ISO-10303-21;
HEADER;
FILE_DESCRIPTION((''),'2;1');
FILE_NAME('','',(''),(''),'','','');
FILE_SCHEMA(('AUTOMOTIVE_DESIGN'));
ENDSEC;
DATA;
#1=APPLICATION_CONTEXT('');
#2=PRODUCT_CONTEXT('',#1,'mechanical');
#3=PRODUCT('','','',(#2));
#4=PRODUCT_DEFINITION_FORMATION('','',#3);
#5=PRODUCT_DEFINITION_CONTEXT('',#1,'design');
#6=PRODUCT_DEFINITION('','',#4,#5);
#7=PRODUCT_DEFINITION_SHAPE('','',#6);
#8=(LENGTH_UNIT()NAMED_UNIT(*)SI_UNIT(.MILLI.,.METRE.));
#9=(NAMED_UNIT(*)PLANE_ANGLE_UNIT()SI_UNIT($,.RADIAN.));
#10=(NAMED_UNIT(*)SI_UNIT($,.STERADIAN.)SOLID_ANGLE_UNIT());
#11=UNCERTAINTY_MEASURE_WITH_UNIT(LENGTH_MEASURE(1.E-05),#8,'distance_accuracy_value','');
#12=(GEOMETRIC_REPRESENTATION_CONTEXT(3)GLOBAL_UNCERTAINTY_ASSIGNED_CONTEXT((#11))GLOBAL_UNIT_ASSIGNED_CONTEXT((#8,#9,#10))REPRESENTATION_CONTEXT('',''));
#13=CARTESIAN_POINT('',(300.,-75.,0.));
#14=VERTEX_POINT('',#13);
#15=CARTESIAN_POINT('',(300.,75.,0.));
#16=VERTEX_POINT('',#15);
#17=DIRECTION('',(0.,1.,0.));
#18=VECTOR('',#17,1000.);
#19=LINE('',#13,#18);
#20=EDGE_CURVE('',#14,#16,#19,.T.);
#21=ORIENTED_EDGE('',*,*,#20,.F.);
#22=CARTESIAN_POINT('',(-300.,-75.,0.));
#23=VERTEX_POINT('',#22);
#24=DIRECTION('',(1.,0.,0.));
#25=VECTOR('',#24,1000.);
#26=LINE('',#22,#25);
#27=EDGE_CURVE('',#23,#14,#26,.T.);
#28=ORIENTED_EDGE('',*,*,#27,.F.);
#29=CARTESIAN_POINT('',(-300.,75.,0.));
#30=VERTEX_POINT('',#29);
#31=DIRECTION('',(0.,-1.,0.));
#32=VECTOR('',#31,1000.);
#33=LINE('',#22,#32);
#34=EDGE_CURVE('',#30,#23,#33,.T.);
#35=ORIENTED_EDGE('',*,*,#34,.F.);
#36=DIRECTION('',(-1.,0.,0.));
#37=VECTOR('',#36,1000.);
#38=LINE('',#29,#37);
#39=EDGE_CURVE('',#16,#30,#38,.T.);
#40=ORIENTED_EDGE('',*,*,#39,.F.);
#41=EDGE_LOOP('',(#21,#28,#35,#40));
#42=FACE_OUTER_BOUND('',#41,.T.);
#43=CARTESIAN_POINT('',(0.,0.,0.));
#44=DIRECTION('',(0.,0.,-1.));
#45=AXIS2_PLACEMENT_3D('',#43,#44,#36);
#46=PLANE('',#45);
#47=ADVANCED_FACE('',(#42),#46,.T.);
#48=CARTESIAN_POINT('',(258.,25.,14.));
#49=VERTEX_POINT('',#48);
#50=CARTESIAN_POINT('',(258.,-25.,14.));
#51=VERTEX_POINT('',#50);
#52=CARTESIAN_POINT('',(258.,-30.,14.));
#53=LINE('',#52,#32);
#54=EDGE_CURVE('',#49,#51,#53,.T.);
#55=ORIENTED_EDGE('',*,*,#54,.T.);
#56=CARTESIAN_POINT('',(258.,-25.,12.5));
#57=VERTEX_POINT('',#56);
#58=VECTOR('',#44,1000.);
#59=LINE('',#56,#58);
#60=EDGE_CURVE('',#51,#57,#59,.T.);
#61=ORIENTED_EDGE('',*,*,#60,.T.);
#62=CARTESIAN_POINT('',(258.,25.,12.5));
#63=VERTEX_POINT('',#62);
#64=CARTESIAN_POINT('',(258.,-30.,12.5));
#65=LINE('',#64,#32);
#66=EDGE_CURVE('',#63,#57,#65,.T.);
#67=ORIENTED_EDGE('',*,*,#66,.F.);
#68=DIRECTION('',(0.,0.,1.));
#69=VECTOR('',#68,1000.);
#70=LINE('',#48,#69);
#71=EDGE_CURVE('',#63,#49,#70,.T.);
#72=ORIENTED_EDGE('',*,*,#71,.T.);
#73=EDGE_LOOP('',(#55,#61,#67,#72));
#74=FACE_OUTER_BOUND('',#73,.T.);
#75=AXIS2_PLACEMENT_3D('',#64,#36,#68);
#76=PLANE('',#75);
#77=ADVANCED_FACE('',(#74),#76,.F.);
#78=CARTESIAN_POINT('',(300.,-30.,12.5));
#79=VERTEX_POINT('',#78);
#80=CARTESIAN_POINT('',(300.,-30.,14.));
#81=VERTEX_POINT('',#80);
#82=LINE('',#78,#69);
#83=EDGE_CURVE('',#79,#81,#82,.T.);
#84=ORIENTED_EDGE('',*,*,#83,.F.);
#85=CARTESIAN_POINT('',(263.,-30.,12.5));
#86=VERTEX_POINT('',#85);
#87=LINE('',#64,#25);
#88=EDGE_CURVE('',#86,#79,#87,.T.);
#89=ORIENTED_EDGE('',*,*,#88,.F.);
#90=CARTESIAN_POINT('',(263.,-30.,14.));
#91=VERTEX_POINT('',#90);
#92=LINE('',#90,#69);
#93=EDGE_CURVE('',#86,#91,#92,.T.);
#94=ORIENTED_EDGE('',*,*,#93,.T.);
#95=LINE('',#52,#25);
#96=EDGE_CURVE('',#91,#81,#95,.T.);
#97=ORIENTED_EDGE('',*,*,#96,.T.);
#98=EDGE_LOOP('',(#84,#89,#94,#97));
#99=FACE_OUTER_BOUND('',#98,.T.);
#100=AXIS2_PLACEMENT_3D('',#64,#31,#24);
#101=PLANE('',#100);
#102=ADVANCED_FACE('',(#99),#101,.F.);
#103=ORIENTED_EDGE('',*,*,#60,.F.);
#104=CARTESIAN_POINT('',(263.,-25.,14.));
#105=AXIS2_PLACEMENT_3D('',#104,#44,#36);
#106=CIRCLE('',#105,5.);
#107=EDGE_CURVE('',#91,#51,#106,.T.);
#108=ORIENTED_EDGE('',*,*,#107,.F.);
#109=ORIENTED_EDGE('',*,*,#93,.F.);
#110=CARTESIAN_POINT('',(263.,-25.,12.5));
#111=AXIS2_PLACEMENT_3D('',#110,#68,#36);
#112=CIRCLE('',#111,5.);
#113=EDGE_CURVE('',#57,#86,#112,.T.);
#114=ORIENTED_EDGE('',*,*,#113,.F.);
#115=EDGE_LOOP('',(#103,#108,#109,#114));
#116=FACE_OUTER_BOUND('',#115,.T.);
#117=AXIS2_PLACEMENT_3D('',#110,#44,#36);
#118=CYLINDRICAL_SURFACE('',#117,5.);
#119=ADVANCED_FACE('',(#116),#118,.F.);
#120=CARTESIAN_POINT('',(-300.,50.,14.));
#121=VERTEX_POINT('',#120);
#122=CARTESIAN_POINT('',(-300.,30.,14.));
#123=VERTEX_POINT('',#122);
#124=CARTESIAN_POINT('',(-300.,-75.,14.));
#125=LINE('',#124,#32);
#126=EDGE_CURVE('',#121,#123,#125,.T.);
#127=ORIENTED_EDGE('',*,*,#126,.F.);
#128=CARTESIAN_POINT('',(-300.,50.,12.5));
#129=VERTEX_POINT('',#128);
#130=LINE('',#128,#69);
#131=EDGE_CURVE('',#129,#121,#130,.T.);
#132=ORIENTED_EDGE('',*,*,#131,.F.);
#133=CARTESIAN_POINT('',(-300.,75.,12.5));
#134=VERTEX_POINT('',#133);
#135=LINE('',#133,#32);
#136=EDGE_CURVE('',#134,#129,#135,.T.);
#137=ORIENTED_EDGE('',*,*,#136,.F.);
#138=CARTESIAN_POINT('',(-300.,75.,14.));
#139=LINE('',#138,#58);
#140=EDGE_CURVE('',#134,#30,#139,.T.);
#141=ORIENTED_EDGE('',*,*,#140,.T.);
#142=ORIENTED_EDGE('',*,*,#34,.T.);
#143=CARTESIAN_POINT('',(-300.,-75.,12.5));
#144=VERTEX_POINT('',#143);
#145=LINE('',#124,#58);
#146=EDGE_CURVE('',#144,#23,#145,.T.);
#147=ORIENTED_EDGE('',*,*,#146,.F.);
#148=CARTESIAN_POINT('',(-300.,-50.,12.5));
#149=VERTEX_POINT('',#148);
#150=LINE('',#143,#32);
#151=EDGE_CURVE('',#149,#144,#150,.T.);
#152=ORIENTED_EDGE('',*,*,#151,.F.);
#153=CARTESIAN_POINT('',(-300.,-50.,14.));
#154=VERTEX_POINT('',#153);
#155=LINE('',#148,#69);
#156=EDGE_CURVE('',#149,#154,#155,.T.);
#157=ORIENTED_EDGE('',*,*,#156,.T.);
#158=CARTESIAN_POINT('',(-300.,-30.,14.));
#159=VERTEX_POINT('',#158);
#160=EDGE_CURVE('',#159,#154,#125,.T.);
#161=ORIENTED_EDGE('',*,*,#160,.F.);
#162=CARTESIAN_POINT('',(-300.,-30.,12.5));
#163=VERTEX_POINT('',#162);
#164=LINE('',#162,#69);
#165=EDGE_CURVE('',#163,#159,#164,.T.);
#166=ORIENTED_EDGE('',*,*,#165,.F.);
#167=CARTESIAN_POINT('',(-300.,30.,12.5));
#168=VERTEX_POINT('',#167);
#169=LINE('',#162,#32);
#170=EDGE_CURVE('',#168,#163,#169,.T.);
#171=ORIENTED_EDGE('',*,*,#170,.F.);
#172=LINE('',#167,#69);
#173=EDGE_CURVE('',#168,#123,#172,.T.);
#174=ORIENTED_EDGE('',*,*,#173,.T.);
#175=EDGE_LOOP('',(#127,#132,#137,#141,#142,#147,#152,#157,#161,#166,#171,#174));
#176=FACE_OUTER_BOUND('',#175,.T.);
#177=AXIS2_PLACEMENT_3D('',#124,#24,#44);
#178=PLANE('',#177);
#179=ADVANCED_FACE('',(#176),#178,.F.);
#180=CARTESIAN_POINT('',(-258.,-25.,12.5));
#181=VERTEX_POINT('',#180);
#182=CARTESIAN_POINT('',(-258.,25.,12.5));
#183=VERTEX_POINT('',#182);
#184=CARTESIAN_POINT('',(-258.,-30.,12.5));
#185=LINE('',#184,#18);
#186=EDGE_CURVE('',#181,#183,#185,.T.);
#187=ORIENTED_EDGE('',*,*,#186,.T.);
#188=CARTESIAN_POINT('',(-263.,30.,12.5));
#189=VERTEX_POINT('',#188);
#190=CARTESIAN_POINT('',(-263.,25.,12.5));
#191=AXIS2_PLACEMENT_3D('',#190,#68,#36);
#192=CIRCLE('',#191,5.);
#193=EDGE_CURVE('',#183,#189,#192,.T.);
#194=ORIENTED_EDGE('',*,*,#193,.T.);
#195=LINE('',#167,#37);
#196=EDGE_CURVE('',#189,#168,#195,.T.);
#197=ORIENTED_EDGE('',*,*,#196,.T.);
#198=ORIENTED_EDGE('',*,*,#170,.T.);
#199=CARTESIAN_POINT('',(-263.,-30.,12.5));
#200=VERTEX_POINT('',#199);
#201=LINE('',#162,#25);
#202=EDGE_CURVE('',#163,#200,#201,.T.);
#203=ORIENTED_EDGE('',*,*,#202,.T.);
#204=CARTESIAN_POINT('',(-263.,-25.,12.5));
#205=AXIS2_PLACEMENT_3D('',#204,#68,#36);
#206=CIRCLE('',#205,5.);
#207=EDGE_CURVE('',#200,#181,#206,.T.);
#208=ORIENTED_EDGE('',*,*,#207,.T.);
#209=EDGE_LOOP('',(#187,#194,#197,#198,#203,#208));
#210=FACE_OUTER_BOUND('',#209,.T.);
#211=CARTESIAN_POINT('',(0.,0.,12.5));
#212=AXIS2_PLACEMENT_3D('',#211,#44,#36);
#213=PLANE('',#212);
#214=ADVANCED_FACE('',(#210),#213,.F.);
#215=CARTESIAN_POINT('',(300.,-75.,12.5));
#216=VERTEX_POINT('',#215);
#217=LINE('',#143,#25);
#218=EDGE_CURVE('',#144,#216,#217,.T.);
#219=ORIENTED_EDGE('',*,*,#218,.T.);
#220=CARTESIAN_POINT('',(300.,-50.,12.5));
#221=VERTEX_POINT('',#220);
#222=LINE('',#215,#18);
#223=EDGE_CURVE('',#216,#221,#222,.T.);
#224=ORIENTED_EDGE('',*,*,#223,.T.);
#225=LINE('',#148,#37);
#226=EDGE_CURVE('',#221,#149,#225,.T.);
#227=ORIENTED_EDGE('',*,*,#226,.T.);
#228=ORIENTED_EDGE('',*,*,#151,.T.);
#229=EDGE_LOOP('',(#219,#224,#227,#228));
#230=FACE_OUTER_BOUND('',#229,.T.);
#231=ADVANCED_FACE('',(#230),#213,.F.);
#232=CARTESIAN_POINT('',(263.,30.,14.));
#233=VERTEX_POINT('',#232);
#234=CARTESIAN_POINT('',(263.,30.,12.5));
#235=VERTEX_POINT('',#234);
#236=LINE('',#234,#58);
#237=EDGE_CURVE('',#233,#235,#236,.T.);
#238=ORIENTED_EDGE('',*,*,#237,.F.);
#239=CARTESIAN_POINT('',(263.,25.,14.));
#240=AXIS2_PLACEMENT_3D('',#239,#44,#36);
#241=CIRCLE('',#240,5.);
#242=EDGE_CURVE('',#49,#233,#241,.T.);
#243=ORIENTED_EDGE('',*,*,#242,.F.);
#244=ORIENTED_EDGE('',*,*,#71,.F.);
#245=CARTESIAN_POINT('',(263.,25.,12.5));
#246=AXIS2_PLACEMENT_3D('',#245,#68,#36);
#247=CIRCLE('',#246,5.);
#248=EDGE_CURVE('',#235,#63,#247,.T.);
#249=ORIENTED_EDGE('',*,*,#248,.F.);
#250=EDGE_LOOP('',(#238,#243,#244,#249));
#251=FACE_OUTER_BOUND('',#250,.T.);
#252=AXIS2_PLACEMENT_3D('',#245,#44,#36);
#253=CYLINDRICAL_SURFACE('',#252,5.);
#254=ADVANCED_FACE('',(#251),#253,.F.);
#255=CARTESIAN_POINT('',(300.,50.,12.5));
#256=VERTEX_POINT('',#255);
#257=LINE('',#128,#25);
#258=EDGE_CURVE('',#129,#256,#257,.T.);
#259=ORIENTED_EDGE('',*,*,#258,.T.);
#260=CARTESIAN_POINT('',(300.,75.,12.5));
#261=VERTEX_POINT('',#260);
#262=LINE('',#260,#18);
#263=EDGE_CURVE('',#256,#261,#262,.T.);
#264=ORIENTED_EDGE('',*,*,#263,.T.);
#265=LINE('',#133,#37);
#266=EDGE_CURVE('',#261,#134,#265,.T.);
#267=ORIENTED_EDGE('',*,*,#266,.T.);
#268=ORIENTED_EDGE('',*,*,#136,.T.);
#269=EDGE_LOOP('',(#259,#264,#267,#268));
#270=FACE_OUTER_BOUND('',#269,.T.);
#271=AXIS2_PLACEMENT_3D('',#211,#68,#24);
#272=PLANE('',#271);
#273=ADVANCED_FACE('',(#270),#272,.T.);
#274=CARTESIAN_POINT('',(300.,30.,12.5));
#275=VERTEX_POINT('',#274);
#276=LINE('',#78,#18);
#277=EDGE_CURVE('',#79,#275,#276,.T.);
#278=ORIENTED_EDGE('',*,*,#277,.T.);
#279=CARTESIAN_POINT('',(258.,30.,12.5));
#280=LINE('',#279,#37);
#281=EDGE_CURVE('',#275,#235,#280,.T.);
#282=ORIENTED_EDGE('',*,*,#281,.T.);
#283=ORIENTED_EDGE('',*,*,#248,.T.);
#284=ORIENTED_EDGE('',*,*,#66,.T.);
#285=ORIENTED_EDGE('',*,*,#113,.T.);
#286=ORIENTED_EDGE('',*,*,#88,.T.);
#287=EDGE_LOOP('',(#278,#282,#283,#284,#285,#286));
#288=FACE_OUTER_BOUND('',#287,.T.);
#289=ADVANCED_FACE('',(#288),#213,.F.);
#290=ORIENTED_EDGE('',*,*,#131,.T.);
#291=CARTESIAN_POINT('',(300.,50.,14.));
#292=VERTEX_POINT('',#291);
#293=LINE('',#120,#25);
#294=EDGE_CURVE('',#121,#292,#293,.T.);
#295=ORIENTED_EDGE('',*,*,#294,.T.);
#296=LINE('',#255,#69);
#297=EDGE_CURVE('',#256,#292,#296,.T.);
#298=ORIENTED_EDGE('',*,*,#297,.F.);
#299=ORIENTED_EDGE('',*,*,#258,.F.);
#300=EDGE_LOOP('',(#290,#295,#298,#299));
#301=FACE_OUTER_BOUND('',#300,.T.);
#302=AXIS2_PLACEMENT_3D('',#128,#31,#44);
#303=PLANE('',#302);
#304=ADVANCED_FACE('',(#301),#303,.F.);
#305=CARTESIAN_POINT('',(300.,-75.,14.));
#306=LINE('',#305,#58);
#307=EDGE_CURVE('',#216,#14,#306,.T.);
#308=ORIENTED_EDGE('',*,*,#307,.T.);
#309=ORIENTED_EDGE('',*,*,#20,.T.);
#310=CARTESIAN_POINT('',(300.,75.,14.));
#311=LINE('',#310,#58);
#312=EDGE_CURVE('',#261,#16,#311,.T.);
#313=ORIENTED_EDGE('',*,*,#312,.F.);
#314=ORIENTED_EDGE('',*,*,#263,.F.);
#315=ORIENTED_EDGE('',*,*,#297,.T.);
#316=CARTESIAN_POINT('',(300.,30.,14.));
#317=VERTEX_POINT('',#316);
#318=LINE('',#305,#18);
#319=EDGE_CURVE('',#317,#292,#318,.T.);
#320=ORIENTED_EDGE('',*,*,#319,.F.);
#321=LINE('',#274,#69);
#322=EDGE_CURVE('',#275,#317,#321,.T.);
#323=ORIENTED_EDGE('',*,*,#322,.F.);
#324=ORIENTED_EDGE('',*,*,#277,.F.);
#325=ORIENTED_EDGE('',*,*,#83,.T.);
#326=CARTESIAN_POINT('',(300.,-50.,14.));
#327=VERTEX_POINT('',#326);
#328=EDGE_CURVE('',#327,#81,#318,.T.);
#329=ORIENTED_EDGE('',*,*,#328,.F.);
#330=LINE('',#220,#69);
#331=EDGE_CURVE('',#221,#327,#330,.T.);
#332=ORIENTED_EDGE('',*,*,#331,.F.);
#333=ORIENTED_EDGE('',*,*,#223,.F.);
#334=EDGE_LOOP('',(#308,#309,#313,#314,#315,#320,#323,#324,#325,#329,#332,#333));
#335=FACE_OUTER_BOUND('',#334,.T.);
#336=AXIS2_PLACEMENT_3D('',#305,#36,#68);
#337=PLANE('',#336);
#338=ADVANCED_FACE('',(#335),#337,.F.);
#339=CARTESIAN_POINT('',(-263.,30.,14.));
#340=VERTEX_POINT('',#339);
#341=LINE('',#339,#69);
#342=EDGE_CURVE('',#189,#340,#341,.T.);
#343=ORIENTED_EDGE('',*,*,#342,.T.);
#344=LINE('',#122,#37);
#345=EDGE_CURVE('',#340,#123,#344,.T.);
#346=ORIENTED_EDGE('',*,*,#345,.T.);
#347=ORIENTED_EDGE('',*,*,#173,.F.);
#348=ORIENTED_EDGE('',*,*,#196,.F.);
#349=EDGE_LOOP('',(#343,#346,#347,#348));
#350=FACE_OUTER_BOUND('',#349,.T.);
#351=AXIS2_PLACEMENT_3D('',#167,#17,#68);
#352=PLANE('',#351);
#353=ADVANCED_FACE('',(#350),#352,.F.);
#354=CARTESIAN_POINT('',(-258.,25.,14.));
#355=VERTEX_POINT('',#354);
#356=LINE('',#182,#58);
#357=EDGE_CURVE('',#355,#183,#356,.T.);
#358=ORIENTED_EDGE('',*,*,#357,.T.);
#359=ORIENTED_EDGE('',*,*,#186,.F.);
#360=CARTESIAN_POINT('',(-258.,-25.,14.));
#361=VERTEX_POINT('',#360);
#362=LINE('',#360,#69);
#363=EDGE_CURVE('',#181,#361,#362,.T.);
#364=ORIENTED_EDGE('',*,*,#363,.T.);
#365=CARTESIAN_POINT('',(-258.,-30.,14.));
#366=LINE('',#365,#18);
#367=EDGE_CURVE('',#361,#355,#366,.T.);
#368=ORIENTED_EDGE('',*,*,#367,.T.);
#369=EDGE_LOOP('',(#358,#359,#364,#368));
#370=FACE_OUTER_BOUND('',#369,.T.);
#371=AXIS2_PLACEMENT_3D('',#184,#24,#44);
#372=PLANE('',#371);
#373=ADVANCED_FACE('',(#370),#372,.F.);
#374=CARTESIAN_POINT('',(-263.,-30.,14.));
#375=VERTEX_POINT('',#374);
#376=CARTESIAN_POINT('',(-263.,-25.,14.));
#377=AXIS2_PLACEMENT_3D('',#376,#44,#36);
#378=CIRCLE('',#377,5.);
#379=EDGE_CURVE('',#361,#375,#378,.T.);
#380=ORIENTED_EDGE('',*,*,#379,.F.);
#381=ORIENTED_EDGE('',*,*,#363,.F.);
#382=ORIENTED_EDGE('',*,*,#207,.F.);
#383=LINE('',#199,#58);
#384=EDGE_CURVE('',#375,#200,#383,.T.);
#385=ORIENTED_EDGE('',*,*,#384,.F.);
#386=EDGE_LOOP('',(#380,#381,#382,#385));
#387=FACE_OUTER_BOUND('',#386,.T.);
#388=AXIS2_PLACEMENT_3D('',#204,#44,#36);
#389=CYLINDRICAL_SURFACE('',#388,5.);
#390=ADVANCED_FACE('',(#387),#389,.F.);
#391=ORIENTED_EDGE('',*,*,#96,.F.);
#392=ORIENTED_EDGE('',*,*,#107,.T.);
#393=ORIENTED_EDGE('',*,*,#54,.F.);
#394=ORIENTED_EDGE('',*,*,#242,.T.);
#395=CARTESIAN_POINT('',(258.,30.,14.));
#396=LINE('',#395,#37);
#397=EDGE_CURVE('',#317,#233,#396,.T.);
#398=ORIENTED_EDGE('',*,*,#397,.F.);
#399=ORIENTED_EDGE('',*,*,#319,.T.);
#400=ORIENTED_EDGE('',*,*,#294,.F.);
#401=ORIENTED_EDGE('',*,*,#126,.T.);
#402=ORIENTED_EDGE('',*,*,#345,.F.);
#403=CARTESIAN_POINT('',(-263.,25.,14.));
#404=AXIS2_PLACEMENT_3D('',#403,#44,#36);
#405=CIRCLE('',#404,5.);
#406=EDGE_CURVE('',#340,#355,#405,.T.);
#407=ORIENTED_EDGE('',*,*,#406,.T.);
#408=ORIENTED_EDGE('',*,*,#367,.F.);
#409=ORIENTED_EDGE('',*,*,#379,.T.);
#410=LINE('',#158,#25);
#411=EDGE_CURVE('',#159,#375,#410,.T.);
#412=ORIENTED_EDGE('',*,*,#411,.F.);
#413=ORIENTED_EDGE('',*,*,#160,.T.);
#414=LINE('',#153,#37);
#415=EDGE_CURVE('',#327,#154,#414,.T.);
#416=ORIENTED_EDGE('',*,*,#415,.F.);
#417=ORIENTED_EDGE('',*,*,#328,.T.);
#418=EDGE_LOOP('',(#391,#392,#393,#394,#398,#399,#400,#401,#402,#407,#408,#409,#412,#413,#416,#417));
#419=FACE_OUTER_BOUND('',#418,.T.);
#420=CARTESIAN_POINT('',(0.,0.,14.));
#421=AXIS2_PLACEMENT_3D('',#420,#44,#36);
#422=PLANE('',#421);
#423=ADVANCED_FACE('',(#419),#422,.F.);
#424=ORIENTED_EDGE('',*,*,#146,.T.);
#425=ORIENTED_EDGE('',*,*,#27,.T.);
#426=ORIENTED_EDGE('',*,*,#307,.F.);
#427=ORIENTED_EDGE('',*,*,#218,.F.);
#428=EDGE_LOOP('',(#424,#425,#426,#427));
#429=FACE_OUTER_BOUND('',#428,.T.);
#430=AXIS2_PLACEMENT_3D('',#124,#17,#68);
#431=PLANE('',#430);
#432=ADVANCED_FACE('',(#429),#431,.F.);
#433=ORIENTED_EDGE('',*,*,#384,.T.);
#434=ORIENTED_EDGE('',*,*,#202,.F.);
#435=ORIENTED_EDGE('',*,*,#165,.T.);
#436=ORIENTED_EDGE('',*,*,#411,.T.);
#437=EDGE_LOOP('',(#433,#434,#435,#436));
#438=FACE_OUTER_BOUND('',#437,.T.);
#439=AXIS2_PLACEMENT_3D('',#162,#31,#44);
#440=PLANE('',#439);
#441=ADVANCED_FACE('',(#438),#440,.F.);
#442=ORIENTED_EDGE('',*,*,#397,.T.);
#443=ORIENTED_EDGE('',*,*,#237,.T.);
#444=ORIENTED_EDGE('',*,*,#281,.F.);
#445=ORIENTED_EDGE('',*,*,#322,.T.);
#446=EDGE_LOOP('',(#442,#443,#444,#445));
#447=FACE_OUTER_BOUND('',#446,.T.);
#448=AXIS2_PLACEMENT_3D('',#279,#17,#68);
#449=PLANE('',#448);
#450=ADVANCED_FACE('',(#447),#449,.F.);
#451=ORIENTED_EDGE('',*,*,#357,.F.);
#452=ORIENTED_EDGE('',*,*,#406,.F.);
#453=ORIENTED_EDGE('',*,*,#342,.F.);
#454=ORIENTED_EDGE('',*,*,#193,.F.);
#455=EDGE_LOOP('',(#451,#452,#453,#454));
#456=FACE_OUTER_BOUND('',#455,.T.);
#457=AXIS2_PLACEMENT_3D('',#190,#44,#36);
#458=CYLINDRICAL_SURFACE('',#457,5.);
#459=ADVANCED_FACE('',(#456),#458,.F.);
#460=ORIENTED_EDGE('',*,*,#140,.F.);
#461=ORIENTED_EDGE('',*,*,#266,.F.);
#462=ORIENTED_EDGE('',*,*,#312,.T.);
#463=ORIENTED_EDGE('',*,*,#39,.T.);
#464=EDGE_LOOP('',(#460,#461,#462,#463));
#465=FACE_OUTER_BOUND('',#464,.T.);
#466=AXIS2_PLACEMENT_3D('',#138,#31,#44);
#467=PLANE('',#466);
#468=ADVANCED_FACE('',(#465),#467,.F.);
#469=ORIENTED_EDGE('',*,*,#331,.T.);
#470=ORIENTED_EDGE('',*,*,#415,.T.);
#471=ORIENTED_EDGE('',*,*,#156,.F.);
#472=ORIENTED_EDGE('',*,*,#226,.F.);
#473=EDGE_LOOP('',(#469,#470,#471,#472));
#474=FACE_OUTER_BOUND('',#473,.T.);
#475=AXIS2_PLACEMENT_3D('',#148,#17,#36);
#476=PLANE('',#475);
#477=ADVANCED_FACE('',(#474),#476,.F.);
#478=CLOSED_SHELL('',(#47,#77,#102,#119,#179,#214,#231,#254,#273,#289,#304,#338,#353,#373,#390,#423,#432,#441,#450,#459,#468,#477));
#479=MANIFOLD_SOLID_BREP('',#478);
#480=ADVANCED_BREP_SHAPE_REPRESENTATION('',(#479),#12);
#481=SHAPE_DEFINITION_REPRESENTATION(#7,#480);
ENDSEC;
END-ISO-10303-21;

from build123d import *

# Parameters (mm, degrees)
SKETCH_1_W          = 600
SKETCH_1_H          = 150
EXTRUDE_1_DEPTH     = 14
SKETCH_2_W          = 600
SKETCH_2_H          = 25
CUT_EXTRUDE_1_DEPTH = 1.5
SKETCH_3_W          = 42
SKETCH_3_H          = 60
CUT_EXTRUDE_2_DEPTH = 1.5
FILLET_1_R          = 5


with BuildPart() as part:
    # 草图1 → 凸台-拉伸1 (new body)
    with BuildSketch(Plane.XY):
        Rectangle(SKETCH_1_W, SKETCH_1_H)
    extrude(amount=EXTRUDE_1_DEPTH)

    # 草图2 → 切除-拉伸1 (cut)
    with BuildSketch(Plane.XY.offset(14)):
        with Locations((0, 62.5)):
            Rectangle(SKETCH_2_W, SKETCH_2_H)
        with Locations((0, -62.5)):
            Rectangle(SKETCH_2_W, SKETCH_2_H)
    extrude(amount=-CUT_EXTRUDE_1_DEPTH, mode=Mode.SUBTRACT)

    # 草图3 → 切除-拉伸2 (cut)
    with BuildSketch(Plane.XY.offset(14)):
        with Locations((-279, 0)):
            Rectangle(SKETCH_3_W, SKETCH_3_H)
        with Locations((279, 0)):
            Rectangle(SKETCH_3_W, SKETCH_3_H)
    extrude(amount=-CUT_EXTRUDE_2_DEPTH, mode=Mode.SUBTRACT)

    # 圆角1
    fillet_1_edges = [part.edges().sort_by_distance(p)[0] for p in [
        (-258, 30, 13.25),
        (-258, -30, 13.25),
        (258, -30, 13.25),
        (258, 30, 13.25),
    ]]
    fillet(fillet_1_edges, radius=FILLET_1_R)


solid = part.part
